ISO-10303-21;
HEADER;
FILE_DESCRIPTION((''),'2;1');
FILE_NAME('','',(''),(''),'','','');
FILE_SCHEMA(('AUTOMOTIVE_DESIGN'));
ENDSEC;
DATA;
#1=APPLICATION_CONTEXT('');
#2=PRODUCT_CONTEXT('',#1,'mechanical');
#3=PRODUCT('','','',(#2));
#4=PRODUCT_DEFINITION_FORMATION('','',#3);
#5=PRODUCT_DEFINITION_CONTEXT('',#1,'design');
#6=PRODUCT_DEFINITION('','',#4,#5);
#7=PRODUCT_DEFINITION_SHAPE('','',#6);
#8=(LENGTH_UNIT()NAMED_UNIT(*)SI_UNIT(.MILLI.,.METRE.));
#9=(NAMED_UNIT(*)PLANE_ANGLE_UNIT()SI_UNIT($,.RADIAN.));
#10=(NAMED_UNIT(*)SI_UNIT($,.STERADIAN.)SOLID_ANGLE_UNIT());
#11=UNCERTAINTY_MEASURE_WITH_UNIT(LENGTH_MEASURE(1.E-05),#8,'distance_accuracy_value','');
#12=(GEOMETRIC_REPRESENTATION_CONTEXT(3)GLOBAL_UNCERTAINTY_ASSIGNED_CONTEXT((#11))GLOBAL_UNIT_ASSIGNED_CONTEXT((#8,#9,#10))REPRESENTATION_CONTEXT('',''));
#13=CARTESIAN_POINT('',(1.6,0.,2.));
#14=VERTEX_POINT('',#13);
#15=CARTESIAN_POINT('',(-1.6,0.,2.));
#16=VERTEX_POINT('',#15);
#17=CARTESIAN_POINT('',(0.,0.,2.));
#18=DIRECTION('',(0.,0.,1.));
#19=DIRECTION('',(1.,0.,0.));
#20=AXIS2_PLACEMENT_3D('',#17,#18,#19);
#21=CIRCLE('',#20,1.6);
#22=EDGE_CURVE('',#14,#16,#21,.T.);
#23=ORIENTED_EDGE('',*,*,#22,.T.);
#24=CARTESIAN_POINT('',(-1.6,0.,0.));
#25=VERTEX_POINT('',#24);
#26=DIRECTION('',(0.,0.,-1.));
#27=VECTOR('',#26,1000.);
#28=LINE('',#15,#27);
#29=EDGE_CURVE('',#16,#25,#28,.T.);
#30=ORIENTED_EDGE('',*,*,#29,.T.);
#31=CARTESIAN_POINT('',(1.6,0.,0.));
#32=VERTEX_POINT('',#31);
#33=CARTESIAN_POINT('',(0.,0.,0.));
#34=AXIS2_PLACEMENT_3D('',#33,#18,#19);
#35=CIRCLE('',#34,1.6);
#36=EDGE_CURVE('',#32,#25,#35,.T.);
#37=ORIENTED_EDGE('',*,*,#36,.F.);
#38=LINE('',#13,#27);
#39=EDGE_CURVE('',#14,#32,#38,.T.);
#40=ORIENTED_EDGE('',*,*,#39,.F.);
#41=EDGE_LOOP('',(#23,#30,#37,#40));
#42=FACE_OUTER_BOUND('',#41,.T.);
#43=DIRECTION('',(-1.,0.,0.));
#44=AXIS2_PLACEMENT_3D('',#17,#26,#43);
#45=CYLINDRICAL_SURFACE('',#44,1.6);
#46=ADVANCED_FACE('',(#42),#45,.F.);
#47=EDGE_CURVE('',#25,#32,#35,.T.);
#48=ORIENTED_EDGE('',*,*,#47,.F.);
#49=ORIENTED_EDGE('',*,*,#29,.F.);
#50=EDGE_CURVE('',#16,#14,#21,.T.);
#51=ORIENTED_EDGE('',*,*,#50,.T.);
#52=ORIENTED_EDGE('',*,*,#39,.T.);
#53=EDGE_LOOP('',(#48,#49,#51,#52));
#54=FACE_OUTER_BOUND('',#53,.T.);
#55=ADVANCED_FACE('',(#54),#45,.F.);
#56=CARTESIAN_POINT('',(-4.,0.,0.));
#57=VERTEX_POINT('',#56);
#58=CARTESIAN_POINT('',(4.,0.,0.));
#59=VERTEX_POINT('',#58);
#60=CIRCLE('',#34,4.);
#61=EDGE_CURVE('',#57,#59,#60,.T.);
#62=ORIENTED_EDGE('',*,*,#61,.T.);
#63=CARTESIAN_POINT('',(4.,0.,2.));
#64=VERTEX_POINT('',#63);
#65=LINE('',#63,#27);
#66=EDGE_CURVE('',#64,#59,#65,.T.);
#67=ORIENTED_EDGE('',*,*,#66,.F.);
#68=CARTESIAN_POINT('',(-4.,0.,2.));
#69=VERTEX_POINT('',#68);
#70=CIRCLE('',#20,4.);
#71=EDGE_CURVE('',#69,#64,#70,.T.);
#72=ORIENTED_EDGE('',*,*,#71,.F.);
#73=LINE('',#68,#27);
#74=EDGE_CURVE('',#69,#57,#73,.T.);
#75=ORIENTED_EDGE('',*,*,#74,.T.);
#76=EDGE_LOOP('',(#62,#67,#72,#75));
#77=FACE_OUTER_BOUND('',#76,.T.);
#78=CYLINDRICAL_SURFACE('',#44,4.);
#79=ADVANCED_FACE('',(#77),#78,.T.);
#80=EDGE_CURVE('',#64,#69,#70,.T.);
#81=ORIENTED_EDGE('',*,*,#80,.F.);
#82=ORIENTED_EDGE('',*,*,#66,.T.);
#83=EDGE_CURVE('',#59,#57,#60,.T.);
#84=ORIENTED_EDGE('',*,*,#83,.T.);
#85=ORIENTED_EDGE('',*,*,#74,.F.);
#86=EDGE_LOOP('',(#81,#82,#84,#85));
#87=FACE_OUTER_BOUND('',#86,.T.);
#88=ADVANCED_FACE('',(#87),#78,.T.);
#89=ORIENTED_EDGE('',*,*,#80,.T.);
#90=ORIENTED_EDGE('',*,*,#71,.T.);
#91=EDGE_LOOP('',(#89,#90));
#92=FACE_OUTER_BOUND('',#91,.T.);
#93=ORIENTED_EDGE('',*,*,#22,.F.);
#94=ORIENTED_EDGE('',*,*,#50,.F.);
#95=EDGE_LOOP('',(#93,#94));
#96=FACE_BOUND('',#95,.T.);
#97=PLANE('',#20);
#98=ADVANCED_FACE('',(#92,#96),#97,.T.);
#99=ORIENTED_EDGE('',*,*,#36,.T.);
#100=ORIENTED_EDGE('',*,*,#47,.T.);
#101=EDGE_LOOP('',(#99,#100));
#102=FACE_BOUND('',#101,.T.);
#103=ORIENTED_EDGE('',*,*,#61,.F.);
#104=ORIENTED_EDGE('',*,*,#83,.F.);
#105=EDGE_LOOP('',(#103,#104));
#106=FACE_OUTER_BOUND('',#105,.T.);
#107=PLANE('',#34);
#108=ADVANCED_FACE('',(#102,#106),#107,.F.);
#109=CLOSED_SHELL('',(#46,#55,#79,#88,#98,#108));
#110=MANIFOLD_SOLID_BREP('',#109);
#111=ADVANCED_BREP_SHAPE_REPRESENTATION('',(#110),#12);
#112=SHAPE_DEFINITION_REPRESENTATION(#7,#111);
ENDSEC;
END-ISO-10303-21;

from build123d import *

# Parameters (mm, degrees)
SKETCH1_R           = 4
SKETCH1_R_2         = 1.6
BOSS_EXTRUDE1_DEPTH = 2


with BuildPart() as part:
    # Sketch1 → Boss-Extrude1 (new body)
    with BuildSketch(Plane.XY):
        Circle(SKETCH1_R)
        Circle(SKETCH1_R_2, mode=Mode.SUBTRACT)
    extrude(amount=BOSS_EXTRUDE1_DEPTH)


solid = part.part
